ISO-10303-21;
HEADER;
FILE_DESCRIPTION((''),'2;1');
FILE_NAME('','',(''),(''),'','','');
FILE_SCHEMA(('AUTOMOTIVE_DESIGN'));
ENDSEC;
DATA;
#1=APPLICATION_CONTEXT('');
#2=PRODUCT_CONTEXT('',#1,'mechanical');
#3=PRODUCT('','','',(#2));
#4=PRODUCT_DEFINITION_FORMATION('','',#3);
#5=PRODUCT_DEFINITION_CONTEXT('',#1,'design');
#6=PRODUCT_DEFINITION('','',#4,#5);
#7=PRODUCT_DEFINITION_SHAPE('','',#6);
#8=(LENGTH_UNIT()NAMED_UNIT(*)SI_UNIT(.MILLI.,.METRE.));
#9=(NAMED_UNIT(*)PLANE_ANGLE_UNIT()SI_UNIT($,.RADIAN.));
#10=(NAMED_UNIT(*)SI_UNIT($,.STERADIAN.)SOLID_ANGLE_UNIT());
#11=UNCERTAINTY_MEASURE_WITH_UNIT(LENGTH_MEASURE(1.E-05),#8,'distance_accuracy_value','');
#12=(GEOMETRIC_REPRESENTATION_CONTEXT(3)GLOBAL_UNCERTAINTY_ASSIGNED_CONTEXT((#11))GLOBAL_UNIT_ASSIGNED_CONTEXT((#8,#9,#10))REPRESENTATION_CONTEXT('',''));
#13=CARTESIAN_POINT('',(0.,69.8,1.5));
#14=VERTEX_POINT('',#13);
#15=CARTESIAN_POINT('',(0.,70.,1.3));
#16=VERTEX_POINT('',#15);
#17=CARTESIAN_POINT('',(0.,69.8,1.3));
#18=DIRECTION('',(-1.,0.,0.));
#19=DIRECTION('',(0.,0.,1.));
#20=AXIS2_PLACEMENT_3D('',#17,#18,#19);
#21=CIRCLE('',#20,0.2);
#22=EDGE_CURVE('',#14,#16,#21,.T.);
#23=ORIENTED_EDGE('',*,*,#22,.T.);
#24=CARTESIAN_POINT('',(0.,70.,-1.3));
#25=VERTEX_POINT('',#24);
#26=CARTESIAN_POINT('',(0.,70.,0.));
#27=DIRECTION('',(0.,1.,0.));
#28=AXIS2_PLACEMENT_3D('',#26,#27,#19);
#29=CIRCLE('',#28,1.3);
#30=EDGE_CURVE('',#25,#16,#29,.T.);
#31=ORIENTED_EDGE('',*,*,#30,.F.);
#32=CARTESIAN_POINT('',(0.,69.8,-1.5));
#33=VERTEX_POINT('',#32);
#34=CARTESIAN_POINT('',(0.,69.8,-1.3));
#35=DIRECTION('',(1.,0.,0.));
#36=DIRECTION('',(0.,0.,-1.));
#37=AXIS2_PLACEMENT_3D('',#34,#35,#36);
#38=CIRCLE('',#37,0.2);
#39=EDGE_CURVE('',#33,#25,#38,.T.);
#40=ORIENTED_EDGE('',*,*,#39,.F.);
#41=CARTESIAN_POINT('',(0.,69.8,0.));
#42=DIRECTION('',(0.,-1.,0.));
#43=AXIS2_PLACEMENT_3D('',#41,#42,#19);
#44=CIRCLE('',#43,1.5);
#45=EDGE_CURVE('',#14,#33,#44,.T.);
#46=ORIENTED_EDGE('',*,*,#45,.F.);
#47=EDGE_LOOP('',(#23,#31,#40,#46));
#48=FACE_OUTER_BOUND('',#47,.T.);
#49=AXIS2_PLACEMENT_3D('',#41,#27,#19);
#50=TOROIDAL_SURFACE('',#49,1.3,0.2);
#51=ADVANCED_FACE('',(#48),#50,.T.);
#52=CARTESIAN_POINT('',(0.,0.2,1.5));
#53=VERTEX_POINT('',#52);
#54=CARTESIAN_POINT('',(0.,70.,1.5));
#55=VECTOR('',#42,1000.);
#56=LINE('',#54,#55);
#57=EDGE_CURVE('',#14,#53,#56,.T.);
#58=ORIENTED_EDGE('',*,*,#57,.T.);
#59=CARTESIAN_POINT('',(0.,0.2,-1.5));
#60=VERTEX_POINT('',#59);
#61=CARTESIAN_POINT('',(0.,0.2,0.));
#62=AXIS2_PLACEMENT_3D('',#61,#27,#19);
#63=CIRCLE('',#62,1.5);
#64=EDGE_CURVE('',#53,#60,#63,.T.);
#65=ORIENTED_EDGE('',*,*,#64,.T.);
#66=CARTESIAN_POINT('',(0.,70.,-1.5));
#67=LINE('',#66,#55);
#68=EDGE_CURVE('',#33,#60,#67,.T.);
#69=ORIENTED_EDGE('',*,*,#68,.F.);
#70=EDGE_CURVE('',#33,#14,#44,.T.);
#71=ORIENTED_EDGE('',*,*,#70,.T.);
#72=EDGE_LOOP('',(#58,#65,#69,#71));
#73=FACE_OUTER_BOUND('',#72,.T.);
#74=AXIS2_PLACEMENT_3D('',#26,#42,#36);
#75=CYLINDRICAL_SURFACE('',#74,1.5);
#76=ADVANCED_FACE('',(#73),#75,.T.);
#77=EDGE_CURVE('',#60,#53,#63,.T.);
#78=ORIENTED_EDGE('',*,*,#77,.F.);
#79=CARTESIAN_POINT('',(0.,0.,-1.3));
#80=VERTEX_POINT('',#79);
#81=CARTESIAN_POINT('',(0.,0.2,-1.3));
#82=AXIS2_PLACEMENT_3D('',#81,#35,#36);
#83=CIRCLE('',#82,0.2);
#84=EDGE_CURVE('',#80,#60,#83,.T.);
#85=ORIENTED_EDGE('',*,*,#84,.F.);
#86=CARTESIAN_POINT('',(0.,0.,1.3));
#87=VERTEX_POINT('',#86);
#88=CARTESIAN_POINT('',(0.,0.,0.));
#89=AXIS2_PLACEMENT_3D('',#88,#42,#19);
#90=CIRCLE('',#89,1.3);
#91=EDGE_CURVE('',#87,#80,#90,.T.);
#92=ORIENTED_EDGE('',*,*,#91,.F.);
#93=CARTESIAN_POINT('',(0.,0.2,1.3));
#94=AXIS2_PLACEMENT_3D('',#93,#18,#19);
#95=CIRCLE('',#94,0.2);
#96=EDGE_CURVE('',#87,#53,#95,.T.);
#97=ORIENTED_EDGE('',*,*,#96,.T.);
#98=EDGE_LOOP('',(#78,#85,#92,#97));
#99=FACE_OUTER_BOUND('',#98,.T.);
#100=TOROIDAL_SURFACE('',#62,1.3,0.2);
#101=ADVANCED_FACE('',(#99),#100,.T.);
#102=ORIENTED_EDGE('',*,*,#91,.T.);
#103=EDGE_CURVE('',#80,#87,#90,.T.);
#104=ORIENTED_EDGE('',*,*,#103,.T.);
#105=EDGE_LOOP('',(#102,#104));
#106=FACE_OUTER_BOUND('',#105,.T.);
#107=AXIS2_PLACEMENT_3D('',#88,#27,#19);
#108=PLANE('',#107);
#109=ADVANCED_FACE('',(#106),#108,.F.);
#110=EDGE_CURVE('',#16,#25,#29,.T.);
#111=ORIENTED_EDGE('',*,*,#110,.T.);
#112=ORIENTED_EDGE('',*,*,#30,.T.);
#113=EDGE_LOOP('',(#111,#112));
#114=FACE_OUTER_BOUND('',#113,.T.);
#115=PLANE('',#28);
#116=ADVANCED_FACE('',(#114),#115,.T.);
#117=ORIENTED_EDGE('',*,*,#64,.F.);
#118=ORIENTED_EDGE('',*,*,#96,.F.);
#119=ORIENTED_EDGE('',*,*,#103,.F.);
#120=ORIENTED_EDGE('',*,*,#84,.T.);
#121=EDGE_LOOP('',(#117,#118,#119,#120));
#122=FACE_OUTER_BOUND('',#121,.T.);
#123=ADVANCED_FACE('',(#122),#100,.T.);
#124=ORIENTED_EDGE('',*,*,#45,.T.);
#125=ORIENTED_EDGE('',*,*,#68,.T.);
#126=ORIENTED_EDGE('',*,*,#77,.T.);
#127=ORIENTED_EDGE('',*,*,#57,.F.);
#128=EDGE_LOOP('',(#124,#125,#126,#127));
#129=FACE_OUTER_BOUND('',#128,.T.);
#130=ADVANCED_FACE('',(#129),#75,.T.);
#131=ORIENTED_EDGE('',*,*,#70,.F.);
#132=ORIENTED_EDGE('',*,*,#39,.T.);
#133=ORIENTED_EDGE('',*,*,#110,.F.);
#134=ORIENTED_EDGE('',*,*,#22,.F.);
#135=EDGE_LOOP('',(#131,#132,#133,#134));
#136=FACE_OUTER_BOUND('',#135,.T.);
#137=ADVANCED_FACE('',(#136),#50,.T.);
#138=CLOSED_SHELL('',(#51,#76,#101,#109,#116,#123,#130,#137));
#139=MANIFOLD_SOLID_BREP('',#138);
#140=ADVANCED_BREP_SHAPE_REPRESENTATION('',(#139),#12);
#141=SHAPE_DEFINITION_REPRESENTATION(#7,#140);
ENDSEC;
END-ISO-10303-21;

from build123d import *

# Parameters (mm, degrees)
SKETCH1_R           = 1.5
BOSS_EXTRUDE1_DEPTH = 70
FILLET1_R           = 0.2


with BuildPart() as part:
    # Sketch1 → Boss-Extrude1 (new body)
    with BuildSketch(Plane(origin=(0, 0, 0), x_dir=(1, 0, 0), z_dir=(0, 1, 0))):
        with Locations(Location((0, 0, 0), (0, 0, 270))):
            Circle(SKETCH1_R)
    extrude(amount=BOSS_EXTRUDE1_DEPTH)

    # Fillet1
    fillet1_edges = [part.edges().sort_by_distance(p)[0] for p in [
        (0, 0, -1.5),
        (0, 70, -1.5),
    ]]
    fillet(fillet1_edges, radius=FILLET1_R)


solid = part.part
